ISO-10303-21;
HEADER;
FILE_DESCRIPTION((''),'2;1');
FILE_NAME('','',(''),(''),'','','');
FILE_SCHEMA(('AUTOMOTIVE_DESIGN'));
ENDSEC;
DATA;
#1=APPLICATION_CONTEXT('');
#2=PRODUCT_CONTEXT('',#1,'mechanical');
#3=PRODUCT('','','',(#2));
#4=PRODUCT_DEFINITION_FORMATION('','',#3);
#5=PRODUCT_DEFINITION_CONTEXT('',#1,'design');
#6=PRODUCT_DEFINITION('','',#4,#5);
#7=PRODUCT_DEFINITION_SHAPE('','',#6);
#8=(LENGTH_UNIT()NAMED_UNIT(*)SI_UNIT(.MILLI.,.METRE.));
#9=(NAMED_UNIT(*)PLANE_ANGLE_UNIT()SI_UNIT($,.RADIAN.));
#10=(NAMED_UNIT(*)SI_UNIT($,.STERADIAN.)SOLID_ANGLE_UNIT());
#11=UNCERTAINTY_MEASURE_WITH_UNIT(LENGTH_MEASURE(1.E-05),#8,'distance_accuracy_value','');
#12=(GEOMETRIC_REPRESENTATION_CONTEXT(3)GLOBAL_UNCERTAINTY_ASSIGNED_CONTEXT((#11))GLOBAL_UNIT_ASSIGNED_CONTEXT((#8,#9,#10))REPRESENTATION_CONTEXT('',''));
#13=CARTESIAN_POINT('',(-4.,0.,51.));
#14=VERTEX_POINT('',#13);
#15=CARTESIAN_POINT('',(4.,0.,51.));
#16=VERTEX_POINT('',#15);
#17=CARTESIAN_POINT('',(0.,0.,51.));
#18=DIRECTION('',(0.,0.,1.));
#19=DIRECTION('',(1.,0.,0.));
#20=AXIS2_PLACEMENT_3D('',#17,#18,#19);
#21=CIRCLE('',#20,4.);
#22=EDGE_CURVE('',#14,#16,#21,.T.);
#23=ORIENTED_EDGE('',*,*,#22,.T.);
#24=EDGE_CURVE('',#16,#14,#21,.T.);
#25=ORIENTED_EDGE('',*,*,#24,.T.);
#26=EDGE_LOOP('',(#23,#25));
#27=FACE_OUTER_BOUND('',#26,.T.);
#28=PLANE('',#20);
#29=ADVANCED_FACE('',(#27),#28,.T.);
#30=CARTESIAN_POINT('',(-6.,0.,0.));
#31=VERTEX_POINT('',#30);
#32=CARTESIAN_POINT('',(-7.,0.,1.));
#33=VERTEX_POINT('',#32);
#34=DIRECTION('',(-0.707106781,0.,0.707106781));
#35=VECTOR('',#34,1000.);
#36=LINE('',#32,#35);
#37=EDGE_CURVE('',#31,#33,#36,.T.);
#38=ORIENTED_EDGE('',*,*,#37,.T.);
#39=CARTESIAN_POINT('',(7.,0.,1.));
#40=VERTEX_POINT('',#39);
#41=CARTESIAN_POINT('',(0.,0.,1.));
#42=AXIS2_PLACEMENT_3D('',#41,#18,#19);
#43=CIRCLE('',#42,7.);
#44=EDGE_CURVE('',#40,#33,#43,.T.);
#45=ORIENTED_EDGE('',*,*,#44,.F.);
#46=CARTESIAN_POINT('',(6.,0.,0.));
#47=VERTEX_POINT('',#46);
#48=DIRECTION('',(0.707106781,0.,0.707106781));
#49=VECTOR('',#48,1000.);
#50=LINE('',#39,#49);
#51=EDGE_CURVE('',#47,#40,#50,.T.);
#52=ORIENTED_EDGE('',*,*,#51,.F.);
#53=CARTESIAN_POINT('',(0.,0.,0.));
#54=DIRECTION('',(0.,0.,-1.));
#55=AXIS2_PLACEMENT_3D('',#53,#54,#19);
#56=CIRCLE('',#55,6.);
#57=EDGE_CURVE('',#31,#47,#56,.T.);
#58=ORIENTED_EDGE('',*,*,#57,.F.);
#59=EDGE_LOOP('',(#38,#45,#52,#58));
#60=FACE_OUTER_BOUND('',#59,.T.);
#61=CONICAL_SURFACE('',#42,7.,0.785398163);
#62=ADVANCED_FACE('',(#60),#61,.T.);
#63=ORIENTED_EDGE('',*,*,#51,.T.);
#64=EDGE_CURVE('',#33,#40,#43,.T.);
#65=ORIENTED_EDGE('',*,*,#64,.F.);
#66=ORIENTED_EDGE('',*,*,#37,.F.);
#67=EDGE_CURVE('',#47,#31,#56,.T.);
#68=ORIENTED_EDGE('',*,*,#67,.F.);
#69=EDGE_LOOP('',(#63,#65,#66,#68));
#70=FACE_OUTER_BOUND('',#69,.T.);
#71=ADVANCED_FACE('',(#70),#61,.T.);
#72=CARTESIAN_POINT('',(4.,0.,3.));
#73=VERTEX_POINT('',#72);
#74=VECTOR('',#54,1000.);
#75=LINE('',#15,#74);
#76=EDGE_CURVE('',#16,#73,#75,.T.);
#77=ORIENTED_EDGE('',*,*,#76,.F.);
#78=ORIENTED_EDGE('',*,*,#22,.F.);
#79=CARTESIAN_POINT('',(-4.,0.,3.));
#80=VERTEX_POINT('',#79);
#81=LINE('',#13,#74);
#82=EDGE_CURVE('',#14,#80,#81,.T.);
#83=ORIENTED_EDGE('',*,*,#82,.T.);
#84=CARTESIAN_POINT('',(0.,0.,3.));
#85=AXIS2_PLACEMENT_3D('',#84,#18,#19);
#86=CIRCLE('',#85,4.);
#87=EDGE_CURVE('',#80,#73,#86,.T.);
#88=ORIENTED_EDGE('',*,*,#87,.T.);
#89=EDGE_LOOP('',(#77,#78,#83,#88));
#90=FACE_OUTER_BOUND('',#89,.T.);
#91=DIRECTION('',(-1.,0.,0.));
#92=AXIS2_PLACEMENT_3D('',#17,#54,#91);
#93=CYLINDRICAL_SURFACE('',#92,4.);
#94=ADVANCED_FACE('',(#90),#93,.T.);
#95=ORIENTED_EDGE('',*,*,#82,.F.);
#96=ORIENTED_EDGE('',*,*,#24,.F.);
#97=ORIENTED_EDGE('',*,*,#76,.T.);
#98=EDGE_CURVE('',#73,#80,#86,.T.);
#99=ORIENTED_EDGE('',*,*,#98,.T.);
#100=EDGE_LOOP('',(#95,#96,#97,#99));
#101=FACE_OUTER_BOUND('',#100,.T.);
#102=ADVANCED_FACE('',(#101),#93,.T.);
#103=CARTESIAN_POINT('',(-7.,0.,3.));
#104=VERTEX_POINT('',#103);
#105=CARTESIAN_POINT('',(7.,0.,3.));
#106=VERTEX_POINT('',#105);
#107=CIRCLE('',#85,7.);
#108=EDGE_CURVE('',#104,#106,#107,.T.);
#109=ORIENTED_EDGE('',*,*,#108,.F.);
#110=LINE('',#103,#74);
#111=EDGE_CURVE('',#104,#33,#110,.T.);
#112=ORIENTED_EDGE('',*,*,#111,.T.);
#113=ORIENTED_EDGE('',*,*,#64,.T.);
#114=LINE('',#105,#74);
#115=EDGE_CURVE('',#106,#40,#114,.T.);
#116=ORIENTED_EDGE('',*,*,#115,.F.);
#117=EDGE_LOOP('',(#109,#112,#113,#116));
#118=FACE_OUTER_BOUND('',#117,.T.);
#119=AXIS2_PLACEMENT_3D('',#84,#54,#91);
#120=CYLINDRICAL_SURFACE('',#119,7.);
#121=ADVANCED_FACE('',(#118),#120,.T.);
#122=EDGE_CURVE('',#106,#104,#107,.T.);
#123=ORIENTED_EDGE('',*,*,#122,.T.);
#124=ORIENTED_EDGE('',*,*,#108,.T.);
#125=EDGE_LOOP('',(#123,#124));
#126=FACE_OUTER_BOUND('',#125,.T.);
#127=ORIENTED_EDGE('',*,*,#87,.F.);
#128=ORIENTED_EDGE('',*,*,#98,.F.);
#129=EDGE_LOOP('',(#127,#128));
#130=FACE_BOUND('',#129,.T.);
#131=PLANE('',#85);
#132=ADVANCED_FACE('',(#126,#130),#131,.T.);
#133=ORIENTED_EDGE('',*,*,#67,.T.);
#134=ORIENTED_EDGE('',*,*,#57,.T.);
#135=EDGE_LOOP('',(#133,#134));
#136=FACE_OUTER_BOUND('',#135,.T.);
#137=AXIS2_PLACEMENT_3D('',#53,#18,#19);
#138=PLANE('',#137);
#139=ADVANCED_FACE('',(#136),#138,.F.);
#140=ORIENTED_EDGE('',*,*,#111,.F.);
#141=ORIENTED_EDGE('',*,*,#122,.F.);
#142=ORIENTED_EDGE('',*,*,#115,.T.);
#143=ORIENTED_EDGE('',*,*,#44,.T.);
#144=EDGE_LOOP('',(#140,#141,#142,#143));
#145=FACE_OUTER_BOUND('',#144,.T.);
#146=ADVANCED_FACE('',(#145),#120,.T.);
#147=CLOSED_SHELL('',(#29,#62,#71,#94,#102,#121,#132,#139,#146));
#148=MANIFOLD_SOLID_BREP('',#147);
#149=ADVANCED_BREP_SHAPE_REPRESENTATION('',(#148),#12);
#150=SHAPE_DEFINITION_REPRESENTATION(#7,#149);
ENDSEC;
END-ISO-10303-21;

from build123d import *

# Parameters (mm, degrees)
HEAD_PROFILE_14_R      = 7
HEAD_14X3_DEPTH        = 3
SHANK_PROFILE_8_R      = 4
SHANK_8X48_DEPTH       = 48
HEAD_CHAMFER_1X45_SIZE = 1


with BuildPart() as part:
    # Head Profile Ø14 → Head Ø14x3 (new body)
    with BuildSketch(Plane.XY):
        Circle(HEAD_PROFILE_14_R)
    extrude(amount=HEAD_14X3_DEPTH)

    # Shank Profile Ø8 → Shank Ø8x48 (add)
    with BuildSketch(Plane.XY.offset(3)):
        Circle(SHANK_PROFILE_8_R)
    extrude(amount=SHANK_8X48_DEPTH)

    # Head Chamfer 1x45°
    head_chamfer_1x45_edges = [part.edges().sort_by_distance(p)[0] for p in [
        (-7, 0, 0),
    ]]
    chamfer(head_chamfer_1x45_edges, length=HEAD_CHAMFER_1X45_SIZE)


solid = part.part
